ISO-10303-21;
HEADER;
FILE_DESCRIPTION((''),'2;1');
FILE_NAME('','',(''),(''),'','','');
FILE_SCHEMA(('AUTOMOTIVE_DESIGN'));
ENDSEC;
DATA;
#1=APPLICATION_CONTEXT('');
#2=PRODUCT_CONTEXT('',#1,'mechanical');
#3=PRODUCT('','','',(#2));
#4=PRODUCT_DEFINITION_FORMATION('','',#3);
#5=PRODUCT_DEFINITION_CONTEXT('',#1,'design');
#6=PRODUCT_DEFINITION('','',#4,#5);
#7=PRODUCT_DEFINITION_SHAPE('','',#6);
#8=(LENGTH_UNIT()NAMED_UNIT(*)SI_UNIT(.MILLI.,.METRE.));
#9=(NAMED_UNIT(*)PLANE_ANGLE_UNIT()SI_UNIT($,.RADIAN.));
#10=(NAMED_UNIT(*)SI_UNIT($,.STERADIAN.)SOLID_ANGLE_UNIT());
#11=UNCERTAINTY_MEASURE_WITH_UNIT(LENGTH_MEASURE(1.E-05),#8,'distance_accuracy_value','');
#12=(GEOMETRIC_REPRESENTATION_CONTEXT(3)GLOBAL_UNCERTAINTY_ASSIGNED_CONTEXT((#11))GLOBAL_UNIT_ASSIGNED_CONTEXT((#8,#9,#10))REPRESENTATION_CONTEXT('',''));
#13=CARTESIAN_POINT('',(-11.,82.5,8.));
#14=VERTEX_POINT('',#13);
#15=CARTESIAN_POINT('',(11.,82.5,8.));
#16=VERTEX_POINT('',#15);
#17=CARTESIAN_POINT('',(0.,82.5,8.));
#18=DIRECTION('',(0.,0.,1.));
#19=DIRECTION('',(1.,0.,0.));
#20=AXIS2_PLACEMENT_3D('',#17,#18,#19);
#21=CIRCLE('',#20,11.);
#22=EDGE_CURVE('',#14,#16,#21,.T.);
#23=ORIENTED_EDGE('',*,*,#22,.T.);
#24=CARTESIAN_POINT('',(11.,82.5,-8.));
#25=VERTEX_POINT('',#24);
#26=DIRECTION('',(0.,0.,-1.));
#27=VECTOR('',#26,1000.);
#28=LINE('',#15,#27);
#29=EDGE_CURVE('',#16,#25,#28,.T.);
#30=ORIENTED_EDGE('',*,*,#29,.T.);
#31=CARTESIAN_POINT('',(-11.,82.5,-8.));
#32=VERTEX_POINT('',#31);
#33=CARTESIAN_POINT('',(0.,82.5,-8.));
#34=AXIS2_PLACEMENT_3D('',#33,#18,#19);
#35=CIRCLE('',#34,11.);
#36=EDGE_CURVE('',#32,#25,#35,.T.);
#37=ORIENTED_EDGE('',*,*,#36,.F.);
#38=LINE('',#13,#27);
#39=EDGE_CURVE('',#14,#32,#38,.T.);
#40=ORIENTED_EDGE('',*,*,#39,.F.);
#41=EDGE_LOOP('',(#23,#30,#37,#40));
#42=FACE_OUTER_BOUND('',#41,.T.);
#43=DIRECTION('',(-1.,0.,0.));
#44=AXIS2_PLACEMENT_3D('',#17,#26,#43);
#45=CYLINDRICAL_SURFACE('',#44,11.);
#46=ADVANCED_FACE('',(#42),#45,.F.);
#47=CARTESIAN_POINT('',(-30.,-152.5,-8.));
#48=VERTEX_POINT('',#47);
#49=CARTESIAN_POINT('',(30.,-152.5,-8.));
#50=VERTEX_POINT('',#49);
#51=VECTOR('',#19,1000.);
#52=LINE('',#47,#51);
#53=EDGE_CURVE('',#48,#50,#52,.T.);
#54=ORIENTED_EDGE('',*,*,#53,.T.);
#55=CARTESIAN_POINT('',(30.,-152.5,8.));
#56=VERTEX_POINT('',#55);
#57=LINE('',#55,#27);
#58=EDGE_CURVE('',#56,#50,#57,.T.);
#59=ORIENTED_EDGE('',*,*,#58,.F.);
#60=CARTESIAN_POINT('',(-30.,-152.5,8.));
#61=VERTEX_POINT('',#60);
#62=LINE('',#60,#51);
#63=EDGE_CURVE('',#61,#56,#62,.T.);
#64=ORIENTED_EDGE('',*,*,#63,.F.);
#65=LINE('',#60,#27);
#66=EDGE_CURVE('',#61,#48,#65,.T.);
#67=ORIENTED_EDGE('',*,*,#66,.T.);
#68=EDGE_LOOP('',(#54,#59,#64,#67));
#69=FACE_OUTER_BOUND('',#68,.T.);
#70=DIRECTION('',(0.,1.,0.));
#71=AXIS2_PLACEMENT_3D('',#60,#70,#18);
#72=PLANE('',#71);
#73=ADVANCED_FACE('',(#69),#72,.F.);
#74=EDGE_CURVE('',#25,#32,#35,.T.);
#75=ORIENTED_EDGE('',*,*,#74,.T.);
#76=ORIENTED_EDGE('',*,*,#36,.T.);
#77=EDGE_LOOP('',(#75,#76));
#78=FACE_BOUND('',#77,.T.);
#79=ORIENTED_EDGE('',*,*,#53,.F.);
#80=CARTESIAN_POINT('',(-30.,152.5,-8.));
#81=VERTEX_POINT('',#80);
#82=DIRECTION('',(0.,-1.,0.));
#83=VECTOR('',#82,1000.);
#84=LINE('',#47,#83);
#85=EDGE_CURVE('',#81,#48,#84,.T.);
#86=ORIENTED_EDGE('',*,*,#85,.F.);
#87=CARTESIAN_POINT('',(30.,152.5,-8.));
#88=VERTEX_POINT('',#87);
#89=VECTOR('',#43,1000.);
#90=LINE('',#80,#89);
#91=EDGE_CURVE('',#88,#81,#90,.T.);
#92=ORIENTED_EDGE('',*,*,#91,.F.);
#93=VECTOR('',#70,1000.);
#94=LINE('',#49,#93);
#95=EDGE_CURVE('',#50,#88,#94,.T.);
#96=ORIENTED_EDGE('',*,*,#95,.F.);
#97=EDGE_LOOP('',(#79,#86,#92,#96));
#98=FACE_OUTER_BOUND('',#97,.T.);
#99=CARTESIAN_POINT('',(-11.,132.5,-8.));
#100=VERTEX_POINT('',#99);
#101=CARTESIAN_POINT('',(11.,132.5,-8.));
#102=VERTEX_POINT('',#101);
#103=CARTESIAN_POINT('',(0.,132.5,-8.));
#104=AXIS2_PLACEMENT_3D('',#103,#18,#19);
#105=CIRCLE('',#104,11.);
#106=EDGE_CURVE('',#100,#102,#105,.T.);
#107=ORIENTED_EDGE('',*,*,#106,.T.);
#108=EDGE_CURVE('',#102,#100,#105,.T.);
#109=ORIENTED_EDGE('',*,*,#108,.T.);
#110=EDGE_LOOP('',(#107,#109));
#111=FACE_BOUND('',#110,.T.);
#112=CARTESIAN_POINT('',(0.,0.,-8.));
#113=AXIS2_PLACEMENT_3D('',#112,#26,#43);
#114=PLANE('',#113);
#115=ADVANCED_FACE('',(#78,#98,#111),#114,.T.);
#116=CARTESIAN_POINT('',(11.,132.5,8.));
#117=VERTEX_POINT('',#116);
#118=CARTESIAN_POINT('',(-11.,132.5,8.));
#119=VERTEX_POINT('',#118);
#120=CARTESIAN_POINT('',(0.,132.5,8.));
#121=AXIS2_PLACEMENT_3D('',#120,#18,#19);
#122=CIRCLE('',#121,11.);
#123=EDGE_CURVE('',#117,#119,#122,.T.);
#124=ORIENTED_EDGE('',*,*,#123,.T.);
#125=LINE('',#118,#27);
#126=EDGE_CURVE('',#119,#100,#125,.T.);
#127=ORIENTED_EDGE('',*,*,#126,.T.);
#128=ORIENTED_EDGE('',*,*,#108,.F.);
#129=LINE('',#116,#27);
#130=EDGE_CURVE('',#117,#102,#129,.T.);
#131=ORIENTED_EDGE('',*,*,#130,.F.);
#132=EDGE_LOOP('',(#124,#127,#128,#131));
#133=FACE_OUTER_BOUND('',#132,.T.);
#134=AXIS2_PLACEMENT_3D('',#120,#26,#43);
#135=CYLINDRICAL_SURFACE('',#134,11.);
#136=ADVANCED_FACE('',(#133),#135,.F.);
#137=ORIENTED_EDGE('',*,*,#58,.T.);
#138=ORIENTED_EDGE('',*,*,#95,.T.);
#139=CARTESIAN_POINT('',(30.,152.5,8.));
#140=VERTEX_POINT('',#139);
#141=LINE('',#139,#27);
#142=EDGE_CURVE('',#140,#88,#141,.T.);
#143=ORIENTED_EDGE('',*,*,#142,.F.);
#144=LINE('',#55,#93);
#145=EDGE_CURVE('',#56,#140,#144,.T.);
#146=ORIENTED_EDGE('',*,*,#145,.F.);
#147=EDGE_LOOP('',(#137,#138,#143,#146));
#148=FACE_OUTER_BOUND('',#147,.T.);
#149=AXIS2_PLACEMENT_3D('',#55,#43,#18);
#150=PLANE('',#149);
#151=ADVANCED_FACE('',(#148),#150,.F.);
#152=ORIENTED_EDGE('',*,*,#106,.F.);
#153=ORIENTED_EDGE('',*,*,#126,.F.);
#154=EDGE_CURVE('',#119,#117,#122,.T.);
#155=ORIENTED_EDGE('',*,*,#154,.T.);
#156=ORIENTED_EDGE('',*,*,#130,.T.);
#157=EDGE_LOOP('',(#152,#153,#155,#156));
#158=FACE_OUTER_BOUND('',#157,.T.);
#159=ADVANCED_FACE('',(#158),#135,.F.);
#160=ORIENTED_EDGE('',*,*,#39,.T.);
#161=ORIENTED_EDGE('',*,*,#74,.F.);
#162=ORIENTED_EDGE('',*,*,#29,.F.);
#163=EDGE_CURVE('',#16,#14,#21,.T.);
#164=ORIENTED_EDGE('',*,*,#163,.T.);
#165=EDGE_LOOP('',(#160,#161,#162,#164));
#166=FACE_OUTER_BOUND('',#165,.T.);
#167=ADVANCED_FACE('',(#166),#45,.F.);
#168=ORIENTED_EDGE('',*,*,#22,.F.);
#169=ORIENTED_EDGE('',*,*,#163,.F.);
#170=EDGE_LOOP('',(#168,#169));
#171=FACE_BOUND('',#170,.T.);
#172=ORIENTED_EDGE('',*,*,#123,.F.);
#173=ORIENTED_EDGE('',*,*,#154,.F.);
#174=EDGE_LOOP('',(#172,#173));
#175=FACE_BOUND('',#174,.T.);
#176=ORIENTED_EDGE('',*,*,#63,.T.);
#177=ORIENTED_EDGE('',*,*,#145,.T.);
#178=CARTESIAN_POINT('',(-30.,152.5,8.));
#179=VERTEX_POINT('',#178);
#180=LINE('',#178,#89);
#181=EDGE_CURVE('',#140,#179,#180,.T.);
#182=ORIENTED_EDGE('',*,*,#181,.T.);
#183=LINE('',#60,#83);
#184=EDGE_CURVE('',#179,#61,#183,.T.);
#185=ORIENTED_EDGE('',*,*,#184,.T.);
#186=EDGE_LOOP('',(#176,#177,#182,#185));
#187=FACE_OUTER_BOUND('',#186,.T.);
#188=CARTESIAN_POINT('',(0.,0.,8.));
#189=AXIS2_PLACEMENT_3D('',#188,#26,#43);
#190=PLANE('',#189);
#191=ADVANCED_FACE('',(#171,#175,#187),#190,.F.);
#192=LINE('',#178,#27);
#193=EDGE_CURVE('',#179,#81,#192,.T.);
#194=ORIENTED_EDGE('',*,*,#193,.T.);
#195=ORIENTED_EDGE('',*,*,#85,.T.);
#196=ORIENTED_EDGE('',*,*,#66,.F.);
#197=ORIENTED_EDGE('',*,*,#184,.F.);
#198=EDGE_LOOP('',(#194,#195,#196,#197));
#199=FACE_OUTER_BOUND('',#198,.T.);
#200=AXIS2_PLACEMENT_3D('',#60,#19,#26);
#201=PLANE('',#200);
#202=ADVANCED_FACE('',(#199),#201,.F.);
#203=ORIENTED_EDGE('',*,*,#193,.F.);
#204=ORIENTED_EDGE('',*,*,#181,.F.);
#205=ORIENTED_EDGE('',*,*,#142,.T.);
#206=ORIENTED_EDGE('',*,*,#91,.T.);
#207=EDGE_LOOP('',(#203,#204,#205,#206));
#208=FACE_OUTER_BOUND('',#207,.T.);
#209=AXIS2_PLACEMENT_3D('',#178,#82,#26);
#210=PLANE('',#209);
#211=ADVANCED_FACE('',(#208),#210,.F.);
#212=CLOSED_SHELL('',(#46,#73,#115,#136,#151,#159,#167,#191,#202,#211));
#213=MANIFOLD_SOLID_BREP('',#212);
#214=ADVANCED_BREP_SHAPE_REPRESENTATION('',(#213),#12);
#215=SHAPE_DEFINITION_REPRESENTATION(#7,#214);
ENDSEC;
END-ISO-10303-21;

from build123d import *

# Parameters (mm, degrees)
SKETCH_1_W      = 60
SKETCH_1_H      = 305
SKETCH_1_R      = 11
EXTRUDE_1_DEPTH = 8


with BuildPart() as part:
    # 草图1 → 凸台-拉伸1 (new, symmetric)
    with BuildSketch(Plane.XY):
        Rectangle(SKETCH_1_W, SKETCH_1_H)
        with Locations((0, 132.5)):
            Circle(SKETCH_1_R, mode=Mode.SUBTRACT)
        with Locations((0, 82.5)):
            Circle(SKETCH_1_R, mode=Mode.SUBTRACT)
    extrude(amount=EXTRUDE_1_DEPTH, both=True)


solid = part.part
